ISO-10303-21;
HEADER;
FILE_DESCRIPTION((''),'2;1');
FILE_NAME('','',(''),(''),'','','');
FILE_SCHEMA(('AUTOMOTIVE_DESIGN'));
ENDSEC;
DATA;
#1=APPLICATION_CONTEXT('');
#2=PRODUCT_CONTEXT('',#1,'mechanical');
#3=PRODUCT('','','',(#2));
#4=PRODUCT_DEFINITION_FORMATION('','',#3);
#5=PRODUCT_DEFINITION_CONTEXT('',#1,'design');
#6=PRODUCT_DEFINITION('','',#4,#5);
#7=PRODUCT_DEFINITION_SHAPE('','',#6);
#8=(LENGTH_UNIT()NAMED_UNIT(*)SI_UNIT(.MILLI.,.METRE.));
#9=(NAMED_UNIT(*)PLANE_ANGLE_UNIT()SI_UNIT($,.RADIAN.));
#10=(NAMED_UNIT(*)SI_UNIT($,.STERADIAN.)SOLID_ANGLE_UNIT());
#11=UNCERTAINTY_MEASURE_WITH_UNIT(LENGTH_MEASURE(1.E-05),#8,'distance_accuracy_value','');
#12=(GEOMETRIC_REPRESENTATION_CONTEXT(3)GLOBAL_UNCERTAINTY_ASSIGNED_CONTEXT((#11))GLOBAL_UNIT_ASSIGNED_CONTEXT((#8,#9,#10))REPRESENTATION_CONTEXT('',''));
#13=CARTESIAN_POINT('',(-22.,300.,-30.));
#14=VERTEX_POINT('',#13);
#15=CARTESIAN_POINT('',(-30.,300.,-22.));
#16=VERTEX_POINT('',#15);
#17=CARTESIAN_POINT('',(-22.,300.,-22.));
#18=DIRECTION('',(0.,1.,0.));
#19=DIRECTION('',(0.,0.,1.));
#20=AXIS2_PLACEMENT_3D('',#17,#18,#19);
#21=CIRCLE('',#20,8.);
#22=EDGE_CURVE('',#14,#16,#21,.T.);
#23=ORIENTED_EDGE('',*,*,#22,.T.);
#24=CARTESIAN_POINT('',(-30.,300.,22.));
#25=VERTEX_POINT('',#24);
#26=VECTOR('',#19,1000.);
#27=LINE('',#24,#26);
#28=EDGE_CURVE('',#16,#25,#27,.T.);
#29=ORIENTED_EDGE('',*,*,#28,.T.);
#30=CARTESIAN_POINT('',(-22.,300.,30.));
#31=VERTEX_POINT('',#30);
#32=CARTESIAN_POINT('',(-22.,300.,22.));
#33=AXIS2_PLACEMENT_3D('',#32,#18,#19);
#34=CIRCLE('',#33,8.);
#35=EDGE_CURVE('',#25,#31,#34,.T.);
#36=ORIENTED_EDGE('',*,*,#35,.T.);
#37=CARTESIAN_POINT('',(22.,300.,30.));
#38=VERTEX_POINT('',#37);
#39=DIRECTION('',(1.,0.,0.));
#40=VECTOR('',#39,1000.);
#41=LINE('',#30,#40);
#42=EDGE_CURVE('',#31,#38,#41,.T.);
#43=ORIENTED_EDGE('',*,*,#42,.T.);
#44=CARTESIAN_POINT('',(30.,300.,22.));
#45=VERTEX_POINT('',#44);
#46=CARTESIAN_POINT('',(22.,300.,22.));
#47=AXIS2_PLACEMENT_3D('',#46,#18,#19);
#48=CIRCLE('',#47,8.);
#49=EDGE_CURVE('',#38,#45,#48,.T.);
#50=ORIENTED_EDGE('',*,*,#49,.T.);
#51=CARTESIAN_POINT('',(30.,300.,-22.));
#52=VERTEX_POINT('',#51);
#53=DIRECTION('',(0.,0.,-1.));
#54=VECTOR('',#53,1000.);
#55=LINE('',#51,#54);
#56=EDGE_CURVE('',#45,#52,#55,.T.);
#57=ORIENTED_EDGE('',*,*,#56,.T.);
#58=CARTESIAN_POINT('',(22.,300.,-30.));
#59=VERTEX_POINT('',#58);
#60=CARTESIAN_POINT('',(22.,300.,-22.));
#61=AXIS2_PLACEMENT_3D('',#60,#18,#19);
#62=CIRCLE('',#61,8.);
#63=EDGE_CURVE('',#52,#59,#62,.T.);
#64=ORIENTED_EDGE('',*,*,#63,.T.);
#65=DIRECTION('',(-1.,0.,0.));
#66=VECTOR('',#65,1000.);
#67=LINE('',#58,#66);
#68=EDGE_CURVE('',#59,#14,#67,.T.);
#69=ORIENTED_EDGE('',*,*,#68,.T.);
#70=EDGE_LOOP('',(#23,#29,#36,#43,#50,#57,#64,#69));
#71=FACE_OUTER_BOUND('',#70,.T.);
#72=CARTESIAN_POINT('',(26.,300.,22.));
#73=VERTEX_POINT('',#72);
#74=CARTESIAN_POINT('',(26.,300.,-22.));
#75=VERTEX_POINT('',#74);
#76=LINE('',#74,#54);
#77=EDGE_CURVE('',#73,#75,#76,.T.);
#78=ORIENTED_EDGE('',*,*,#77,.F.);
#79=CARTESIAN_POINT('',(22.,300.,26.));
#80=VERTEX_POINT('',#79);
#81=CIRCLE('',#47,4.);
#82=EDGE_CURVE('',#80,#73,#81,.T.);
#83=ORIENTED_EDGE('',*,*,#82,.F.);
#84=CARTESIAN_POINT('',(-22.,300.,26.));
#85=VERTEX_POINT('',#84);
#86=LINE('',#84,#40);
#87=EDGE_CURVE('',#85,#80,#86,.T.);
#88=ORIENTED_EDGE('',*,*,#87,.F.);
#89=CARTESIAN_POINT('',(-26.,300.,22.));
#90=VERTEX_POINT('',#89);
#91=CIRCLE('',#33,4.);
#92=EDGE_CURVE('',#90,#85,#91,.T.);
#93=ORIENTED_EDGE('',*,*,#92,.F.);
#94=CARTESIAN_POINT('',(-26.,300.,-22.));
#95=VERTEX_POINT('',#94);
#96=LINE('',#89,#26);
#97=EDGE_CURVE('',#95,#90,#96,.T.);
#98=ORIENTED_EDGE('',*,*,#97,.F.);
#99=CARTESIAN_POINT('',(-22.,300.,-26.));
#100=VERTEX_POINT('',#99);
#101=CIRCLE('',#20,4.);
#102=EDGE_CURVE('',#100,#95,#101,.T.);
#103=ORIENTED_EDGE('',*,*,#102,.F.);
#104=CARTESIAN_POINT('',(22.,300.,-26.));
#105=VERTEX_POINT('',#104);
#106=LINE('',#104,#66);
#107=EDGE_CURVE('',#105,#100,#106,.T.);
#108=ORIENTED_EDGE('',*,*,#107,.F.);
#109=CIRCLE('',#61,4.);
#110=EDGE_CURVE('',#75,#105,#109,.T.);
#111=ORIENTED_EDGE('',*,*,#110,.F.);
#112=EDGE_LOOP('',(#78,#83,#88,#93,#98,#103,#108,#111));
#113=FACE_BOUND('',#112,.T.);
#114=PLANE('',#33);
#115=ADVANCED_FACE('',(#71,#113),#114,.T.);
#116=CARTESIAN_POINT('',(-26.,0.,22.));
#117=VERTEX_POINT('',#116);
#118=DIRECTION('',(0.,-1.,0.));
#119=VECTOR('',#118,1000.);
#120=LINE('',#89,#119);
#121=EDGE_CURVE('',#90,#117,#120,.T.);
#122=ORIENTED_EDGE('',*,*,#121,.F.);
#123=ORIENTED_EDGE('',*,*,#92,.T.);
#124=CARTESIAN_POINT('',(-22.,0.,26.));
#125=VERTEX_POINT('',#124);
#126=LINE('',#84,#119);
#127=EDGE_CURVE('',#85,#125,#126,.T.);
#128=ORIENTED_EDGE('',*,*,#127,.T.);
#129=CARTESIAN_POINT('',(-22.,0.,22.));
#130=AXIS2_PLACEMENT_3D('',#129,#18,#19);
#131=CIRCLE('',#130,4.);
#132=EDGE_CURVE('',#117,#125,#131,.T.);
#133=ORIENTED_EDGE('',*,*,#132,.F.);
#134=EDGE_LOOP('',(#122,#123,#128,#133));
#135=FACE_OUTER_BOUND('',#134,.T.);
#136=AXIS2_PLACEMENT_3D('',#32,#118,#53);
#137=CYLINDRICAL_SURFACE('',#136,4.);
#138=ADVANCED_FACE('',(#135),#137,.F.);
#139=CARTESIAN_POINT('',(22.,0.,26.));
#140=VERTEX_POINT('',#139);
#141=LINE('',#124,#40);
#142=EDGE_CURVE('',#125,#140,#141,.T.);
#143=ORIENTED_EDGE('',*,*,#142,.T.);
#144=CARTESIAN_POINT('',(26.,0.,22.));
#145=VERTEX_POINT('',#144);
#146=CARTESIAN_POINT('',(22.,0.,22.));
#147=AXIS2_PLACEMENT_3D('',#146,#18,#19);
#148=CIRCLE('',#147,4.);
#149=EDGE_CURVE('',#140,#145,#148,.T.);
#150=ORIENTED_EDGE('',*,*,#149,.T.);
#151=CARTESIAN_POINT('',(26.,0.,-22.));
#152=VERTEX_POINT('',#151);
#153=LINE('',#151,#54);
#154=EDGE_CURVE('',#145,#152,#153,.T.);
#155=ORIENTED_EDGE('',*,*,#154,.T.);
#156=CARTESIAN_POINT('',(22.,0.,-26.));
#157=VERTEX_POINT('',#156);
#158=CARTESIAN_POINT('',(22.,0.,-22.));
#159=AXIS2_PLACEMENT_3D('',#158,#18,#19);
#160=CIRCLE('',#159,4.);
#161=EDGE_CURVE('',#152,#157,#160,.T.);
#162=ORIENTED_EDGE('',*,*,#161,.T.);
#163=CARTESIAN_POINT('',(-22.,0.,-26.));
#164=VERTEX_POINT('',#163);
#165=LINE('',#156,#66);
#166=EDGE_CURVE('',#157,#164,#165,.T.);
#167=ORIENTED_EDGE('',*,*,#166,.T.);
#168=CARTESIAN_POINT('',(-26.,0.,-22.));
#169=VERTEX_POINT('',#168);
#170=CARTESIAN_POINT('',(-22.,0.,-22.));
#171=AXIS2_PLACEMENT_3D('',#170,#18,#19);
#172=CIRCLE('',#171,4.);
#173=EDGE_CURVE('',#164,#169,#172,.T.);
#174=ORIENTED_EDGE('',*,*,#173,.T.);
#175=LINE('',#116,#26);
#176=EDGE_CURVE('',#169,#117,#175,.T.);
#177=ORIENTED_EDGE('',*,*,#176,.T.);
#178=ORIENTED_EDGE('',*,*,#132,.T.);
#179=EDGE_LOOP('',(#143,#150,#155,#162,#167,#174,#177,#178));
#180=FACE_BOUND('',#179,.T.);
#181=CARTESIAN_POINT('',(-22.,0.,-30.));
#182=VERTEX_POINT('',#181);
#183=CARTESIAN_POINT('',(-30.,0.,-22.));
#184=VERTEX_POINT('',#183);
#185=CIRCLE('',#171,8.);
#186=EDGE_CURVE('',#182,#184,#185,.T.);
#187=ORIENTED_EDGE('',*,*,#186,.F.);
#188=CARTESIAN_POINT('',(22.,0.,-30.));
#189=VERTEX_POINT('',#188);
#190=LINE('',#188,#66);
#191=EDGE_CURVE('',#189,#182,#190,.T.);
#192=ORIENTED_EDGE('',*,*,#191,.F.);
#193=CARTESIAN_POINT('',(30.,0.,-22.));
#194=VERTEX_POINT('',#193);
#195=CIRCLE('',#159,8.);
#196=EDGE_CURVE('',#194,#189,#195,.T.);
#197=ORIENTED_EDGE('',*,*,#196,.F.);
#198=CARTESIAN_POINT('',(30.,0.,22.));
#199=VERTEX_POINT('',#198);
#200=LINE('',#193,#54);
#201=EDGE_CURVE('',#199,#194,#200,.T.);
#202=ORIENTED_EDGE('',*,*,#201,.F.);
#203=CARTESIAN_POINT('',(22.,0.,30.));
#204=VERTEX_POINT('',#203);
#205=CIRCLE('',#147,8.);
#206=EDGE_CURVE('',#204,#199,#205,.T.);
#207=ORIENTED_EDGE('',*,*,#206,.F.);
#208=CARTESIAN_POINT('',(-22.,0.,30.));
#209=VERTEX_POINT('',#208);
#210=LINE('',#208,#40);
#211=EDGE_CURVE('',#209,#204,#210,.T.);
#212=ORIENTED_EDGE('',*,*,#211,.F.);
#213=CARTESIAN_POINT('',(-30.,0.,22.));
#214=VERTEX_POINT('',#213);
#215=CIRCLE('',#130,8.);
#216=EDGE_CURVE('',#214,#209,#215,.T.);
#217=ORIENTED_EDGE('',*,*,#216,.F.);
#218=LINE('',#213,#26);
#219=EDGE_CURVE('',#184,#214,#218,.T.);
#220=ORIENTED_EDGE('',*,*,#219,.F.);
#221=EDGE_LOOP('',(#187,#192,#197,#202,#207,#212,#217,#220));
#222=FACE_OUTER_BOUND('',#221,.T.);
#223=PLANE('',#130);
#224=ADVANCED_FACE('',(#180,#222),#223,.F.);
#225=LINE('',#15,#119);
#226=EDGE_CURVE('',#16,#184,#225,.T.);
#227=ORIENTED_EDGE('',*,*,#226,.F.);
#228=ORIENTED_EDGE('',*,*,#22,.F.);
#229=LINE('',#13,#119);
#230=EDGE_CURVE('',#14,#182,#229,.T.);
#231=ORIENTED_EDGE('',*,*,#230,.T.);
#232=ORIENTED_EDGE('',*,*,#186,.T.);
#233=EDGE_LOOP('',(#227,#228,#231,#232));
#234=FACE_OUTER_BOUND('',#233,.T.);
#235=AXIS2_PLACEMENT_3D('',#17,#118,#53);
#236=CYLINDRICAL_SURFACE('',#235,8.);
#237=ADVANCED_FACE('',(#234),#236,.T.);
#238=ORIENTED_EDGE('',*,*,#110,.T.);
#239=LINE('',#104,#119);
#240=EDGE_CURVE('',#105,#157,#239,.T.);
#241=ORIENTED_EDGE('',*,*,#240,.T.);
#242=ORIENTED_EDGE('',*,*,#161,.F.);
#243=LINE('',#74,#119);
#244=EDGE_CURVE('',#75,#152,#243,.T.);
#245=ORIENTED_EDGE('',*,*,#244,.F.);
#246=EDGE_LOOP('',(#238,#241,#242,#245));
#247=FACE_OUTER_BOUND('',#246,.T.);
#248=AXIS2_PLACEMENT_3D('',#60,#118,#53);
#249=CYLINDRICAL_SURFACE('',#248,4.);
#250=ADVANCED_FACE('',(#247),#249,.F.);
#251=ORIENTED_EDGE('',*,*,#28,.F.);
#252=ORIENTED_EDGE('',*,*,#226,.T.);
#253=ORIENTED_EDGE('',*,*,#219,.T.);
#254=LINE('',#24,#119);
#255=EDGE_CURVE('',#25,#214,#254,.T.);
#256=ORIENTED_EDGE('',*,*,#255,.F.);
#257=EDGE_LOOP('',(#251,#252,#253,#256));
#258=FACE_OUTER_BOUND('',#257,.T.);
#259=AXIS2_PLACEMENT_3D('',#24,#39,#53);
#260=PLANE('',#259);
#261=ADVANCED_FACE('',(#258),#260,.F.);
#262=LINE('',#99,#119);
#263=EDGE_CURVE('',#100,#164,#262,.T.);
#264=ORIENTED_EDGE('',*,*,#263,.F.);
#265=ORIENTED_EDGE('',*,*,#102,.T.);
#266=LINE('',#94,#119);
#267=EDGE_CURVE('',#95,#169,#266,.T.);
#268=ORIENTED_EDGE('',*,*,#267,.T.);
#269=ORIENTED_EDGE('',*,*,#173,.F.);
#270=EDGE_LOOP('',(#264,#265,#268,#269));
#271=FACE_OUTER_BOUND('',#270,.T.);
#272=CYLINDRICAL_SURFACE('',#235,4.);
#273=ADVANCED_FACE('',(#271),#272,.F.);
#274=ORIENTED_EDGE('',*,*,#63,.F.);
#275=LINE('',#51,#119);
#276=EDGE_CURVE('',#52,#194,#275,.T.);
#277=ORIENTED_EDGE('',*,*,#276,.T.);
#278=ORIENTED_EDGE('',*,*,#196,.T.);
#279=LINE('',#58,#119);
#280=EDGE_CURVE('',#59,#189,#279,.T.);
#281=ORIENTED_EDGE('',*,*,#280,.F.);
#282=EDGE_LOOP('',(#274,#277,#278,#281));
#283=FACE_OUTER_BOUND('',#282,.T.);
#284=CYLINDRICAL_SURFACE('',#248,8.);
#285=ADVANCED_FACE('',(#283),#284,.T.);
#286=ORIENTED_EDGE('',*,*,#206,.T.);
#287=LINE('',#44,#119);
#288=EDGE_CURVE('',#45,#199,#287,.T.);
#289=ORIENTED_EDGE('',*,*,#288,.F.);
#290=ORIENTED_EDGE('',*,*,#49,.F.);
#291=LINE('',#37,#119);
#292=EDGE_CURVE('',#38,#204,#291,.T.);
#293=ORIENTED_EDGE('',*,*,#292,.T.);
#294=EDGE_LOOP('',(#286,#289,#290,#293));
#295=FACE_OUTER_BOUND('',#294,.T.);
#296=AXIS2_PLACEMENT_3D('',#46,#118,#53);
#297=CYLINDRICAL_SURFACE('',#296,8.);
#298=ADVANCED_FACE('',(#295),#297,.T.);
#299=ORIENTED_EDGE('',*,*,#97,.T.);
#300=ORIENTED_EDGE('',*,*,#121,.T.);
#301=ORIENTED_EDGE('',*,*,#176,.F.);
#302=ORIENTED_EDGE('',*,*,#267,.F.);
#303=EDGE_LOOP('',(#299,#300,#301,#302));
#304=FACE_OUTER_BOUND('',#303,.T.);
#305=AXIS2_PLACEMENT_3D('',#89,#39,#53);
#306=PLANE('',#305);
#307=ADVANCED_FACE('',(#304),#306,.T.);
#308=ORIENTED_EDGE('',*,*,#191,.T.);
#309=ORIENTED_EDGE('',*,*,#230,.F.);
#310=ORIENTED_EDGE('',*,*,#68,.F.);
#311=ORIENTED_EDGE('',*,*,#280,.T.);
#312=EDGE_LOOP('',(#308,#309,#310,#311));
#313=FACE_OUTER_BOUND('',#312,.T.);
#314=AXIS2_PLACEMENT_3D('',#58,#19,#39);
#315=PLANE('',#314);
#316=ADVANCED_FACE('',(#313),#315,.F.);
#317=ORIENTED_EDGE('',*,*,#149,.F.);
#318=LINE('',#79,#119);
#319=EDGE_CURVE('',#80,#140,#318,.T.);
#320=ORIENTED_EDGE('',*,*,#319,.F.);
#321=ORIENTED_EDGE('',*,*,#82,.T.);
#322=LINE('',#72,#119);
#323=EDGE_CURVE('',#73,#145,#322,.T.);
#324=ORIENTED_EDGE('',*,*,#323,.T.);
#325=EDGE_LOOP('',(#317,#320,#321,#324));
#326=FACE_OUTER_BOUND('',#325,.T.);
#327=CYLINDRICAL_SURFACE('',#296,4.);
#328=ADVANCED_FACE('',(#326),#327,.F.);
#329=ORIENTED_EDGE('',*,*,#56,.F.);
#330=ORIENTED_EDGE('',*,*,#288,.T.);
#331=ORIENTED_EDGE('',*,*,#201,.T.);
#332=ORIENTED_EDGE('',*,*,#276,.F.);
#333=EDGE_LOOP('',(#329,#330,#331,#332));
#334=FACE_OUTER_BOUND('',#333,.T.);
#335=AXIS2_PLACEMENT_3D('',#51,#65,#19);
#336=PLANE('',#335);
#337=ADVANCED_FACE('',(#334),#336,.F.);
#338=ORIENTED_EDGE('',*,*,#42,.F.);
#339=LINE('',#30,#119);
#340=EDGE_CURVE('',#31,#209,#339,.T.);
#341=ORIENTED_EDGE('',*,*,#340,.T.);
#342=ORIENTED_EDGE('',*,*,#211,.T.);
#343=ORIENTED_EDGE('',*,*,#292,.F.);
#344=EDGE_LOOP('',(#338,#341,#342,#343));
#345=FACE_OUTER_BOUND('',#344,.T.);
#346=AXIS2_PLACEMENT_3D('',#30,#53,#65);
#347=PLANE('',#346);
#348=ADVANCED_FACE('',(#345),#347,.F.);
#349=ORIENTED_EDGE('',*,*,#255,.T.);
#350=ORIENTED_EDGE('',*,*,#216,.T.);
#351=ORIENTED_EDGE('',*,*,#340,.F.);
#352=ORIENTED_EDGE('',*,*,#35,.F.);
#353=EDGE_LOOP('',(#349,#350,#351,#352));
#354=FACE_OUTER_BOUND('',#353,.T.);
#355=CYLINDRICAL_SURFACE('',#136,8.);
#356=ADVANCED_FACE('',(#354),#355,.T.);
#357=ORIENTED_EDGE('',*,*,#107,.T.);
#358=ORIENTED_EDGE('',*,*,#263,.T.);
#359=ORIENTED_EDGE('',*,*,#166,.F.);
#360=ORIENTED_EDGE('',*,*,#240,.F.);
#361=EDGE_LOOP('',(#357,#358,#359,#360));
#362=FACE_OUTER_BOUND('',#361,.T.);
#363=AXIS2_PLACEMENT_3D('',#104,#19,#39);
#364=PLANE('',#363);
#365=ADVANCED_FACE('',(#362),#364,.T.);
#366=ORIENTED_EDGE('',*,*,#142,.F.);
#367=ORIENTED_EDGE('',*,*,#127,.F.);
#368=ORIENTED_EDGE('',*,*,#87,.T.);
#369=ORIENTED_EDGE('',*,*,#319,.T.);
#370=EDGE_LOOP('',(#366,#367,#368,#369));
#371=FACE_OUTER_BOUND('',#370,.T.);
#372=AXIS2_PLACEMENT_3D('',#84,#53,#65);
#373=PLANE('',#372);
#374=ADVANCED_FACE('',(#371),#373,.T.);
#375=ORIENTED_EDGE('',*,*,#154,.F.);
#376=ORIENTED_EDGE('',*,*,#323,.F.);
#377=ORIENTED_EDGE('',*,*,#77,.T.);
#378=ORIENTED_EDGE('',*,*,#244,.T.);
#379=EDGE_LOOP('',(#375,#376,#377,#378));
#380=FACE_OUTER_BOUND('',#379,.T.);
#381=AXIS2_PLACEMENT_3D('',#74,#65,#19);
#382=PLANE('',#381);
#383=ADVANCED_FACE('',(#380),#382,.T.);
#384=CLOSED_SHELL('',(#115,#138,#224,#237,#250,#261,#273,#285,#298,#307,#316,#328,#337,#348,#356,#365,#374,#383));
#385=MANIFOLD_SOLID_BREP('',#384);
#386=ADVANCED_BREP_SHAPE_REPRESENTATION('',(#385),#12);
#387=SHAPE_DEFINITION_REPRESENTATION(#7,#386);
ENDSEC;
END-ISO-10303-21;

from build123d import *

# Parameters (mm, degrees)
GB_T_6728_2002_SQUARE_HOLLOW_SECTION_60_DEPTH = 300


with BuildPart() as part:
    # Sketch1 → GB/T 6728-2002 square hollow section 60×60×4(1) (new body)
    with BuildSketch(Plane(origin=(0, 0, 0), x_dir=(-1, 0, 0), z_dir=(0, 1, 0))):
        with BuildLine():
            Line((-22, -30), (22, -30))
            ThreePointArc((22, -30), (27.656854249, -27.656854249), (30, -22))
            Line((30, -22), (30, 22))
            ThreePointArc((30, 22), (27.656854249, 27.656854249), (22, 30))
            Line((22, 30), (-22, 30))
            ThreePointArc((-22, 30), (-27.656854249, 27.656854249), (-30, 22))
            Line((-30, 22), (-30, -22))
            ThreePointArc((-30, -22), (-27.656854249, -27.656854249), (-22, -30))
        make_face()
        with BuildLine():
            Line((-22, -26), (22, -26))
            ThreePointArc((22, -26), (24.828427125, -24.828427125), (26, -22))
            Line((26, -22), (26, 22))
            ThreePointArc((26, 22), (24.828427125, 24.828427125), (22, 26))
            Line((22, 26), (-22, 26))
            ThreePointArc((-22, 26), (-24.828427125, 24.828427125), (-26, 22))
            Line((-26, 22), (-26, -22))
            ThreePointArc((-26, -22), (-24.828427125, -24.828427125), (-22, -26))
        make_face(mode=Mode.SUBTRACT)
    extrude(amount=GB_T_6728_2002_SQUARE_HOLLOW_SECTION_60_DEPTH)


solid = part.part
